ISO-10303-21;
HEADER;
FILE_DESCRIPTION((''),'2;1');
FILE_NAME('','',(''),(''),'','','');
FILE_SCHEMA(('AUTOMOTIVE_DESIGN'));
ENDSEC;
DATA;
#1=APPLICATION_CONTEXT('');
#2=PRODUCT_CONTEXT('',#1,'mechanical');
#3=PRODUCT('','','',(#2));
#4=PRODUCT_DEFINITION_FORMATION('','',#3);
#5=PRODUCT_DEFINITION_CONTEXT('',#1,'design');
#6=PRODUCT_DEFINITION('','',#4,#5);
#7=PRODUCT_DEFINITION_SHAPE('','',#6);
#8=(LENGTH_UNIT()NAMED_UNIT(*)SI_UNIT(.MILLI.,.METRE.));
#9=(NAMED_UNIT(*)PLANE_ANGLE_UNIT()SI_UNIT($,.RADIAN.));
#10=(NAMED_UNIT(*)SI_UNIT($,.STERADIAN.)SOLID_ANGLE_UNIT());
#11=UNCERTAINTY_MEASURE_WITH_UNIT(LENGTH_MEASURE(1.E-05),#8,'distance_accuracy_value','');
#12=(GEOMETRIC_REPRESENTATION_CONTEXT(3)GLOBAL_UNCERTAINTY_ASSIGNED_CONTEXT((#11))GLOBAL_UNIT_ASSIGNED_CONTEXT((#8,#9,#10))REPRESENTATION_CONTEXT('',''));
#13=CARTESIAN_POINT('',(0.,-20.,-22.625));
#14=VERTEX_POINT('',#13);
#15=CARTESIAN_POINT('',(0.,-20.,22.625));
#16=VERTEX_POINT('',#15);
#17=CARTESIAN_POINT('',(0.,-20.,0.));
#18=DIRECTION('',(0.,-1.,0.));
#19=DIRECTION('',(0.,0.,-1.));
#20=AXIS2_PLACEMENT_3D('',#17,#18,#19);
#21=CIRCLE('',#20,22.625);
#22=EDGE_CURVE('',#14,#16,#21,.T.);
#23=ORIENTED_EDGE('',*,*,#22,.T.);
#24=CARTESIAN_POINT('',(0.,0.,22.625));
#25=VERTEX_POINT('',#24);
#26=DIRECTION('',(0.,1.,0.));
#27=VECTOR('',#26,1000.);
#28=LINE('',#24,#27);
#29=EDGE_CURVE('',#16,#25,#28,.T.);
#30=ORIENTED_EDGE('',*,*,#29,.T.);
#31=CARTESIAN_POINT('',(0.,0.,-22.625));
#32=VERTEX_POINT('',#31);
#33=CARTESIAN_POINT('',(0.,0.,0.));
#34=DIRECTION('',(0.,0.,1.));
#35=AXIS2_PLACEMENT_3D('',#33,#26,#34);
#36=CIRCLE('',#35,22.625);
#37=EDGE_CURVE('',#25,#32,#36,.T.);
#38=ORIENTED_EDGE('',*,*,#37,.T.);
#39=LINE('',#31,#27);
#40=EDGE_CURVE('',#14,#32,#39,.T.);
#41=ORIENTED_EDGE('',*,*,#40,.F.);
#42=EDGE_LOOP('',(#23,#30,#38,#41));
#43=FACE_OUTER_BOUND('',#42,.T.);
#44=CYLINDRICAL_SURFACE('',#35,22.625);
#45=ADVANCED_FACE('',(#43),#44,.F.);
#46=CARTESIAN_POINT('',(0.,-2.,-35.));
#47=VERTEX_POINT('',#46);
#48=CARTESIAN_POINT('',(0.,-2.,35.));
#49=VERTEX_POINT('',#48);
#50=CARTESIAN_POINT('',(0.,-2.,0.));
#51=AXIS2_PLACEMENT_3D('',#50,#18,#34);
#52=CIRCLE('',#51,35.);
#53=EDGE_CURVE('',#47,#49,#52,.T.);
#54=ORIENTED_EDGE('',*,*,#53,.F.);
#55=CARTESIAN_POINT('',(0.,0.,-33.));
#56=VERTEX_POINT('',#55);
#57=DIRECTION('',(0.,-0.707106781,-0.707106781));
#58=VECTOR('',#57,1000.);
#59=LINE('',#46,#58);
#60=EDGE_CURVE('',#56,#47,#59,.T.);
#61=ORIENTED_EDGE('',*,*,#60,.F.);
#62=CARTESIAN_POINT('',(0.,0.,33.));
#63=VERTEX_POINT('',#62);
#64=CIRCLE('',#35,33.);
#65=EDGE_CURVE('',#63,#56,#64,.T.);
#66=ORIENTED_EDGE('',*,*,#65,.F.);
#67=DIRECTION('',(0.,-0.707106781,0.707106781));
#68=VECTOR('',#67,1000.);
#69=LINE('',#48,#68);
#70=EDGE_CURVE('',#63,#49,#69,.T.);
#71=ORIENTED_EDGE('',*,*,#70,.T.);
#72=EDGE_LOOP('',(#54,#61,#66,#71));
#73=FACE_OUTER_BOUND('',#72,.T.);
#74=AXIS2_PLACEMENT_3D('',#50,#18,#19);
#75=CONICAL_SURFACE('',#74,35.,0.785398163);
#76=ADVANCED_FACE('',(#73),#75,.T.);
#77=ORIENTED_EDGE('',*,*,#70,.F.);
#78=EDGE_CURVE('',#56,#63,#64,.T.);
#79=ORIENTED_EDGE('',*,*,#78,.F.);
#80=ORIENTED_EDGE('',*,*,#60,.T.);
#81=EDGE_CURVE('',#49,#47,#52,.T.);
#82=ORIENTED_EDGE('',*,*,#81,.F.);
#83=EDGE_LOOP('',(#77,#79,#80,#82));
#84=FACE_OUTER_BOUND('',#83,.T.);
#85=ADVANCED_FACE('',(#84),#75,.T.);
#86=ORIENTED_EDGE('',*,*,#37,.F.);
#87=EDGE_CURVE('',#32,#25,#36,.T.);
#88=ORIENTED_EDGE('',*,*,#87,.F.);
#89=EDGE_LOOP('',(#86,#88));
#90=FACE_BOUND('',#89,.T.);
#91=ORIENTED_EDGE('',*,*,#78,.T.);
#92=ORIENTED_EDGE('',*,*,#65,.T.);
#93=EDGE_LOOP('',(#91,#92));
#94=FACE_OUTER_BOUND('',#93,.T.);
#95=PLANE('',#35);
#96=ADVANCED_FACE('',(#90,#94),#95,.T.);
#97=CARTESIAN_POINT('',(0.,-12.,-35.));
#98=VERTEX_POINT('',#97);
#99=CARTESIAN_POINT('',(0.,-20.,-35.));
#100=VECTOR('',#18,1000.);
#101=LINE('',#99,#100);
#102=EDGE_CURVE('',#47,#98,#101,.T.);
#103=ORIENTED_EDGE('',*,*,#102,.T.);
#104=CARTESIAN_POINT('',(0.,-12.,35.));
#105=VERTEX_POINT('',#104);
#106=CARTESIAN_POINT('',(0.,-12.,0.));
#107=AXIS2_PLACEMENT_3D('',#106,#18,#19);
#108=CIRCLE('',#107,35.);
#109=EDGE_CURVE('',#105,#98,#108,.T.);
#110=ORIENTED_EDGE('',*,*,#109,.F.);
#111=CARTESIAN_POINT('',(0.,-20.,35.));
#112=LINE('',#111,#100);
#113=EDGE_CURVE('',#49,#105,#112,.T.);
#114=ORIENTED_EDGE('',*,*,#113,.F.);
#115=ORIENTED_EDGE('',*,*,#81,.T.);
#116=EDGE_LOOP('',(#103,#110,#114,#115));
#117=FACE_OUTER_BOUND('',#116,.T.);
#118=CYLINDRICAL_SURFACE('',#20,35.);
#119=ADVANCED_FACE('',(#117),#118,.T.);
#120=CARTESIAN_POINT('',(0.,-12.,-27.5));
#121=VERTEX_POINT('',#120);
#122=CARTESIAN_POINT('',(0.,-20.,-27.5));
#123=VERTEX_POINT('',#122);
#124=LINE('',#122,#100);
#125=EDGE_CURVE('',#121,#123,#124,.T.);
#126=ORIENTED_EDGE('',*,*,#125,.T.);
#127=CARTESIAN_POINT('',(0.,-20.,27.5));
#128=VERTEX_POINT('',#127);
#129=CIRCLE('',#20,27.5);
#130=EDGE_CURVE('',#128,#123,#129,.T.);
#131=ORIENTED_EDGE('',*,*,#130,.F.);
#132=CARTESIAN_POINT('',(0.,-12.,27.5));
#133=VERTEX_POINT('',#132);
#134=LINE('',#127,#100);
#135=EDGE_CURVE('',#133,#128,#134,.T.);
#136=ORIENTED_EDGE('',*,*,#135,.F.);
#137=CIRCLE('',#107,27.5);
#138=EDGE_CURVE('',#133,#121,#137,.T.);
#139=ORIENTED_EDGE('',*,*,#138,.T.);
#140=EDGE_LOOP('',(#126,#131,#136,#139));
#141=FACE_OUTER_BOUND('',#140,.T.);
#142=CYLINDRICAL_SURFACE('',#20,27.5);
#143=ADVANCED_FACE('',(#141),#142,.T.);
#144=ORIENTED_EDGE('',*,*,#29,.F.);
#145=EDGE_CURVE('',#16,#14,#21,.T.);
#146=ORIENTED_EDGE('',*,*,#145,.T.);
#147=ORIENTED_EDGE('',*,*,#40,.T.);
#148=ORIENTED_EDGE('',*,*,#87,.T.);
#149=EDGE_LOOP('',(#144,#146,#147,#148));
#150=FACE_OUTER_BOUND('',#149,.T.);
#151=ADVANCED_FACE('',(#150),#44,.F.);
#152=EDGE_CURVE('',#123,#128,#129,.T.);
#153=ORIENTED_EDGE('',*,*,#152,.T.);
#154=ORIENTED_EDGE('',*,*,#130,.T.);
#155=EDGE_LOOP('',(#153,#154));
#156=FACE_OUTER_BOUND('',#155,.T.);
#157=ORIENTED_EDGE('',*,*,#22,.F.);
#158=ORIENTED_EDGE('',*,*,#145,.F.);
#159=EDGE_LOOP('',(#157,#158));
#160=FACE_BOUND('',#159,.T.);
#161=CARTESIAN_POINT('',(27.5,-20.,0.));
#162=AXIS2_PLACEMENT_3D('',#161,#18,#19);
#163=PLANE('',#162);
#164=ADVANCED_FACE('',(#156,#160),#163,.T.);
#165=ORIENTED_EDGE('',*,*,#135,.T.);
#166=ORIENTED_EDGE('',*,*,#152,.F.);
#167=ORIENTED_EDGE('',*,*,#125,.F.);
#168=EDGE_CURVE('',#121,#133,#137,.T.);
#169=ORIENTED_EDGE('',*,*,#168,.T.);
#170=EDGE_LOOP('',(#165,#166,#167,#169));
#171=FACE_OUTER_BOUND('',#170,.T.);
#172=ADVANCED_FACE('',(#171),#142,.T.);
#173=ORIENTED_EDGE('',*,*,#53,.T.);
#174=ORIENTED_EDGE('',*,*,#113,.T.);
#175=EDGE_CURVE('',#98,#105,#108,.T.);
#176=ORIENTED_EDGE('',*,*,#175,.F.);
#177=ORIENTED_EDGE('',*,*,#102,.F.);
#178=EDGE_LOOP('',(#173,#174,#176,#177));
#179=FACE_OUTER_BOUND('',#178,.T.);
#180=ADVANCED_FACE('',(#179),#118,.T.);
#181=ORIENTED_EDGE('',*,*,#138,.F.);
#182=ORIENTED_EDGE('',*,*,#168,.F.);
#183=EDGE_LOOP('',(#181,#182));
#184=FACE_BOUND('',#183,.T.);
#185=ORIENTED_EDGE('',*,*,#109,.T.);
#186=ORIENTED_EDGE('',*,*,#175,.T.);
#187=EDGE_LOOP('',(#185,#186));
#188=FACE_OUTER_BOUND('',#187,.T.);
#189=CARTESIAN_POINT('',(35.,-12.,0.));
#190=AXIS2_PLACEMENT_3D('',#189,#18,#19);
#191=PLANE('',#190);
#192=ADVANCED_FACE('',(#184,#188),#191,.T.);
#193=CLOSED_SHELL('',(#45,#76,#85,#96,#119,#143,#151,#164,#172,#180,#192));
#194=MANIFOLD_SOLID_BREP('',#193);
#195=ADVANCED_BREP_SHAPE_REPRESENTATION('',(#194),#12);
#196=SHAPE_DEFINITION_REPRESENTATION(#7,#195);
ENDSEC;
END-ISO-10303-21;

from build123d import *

# Parameters (mm, degrees)
G1_1_2_TAPPED_HOLE1_D     = 45.25
G1_1_2_TAPPED_HOLE1_DEPTH = 102.54
G1_1_2_TAPPED_HOLE1_TIP   = 13.594471505
CHAMFER1_SIZE             = 2


with BuildPart() as part:
    # Sketch1 → Revolve1 (revolve)
    with BuildSketch(Plane.XY, mode=Mode.PRIVATE) as revolve1_sk:
        Polygon((0, 0), (35, 0), (35, -12), (27.5, -12), (27.5, -20), (0, -20), align=None)
    revolve(revolve1_sk.sketch.rotate(Axis((0, -20, 0), (0, 1, 0)), 90), axis=Axis((0, -20, 0), (0, 1, 0)))

    # G1-1/2 Tapped Hole1
    with Locations(Plane(origin=(0, 0, 0), x_dir=(1, 0, 0), z_dir=(0, 1, 0))):
        with Locations((0, 0)):
            Hole(G1_1_2_TAPPED_HOLE1_D / 2, depth=G1_1_2_TAPPED_HOLE1_DEPTH)
            with Locations((0, 0, -(G1_1_2_TAPPED_HOLE1_DEPTH + G1_1_2_TAPPED_HOLE1_TIP / 2))):  # 118° drill point
                Cone(0, G1_1_2_TAPPED_HOLE1_D / 2, G1_1_2_TAPPED_HOLE1_TIP, mode=Mode.SUBTRACT)

    # Chamfer1
    chamfer1_edges = [part.edges().sort_by_distance(p)[0] for p in [
        (0, 0, 35),
    ]]
    chamfer(chamfer1_edges, length=CHAMFER1_SIZE)


solid = part.part
